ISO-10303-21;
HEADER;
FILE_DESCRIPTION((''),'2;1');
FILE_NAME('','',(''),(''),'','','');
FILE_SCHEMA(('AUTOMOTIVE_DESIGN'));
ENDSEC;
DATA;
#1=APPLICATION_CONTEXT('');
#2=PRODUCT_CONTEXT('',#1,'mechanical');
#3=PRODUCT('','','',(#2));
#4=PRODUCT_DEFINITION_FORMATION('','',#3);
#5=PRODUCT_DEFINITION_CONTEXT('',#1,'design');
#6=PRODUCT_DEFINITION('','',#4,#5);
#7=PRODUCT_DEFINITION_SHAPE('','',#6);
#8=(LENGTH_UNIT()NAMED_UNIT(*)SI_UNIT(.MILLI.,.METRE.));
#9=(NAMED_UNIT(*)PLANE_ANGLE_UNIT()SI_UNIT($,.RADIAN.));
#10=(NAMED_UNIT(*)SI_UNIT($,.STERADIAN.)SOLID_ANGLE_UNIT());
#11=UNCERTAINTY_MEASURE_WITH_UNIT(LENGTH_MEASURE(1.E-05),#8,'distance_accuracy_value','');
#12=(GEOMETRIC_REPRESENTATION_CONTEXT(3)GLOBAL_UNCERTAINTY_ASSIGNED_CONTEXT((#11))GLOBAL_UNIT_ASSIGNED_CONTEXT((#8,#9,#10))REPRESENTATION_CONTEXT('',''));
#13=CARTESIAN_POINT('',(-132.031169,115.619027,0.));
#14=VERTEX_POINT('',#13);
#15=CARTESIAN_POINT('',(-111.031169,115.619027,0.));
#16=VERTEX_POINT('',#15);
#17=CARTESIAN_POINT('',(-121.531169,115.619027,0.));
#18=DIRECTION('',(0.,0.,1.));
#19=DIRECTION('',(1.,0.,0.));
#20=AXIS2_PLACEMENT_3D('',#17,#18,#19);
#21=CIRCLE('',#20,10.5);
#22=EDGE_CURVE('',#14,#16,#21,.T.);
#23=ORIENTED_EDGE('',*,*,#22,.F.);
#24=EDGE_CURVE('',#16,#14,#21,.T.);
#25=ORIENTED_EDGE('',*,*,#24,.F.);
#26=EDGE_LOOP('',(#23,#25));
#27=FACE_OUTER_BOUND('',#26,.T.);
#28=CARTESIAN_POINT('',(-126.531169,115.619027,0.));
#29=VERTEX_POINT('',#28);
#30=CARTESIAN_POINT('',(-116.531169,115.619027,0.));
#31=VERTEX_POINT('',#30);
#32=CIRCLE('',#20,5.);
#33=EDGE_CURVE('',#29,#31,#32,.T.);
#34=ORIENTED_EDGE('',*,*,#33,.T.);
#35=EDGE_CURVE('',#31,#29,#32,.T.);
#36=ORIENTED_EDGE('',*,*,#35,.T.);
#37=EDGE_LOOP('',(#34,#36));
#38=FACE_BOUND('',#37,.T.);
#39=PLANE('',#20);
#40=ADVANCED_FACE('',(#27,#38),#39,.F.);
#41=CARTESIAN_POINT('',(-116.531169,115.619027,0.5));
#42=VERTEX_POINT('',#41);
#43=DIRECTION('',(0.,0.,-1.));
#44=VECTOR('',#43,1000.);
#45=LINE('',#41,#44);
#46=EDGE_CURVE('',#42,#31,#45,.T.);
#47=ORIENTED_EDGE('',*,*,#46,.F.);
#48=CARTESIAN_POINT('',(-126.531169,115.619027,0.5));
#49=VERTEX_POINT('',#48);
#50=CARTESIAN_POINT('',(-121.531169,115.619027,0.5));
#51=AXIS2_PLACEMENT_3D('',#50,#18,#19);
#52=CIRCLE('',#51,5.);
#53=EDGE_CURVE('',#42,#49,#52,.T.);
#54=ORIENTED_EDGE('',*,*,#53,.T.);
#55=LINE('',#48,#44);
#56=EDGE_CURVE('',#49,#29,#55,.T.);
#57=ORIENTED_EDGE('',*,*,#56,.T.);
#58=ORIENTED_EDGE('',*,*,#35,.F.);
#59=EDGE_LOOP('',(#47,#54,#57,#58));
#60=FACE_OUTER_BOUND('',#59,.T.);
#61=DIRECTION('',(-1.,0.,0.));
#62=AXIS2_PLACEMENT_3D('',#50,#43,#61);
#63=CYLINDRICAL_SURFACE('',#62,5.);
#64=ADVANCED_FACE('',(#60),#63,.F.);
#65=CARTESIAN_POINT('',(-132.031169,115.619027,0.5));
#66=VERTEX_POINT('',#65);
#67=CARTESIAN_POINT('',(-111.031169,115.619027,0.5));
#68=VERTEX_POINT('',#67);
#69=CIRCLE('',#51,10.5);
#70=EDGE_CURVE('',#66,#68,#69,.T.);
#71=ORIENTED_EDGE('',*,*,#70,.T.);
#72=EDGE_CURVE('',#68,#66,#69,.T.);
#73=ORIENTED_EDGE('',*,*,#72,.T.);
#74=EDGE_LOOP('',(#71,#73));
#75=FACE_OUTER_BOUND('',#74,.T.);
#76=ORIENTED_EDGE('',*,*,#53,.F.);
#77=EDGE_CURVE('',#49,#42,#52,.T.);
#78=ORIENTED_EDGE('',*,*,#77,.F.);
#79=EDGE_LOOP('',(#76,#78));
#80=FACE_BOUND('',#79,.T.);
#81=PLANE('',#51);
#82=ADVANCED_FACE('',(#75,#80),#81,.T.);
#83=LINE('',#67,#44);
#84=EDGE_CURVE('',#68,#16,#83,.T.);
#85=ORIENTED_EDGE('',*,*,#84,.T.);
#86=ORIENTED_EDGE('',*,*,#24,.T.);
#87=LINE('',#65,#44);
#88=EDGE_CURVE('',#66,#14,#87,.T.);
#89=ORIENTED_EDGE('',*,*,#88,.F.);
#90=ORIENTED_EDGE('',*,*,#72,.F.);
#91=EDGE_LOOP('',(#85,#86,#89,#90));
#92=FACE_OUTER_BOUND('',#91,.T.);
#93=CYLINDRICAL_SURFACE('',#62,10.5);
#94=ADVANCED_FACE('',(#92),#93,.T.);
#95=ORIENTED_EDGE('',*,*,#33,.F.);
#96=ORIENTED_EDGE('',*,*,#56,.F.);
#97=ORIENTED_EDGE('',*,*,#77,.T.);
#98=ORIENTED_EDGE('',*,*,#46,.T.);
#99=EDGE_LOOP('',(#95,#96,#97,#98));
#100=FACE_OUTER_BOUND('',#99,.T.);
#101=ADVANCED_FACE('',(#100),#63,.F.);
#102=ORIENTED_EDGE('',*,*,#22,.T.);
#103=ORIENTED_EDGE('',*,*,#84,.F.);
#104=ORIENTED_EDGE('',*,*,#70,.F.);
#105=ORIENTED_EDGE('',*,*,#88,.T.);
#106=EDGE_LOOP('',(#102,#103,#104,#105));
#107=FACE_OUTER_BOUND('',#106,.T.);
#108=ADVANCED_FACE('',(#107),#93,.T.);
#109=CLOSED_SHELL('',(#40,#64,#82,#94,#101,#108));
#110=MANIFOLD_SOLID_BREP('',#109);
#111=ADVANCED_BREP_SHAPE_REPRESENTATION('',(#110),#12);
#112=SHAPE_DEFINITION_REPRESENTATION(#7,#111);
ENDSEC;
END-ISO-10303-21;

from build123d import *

# Parameters (mm, degrees)
SKETCH1_R           = 10.5
SKETCH1_R_2         = 5
BOSS_EXTRUDE1_DEPTH = 0.5


with BuildPart() as part:
    # Sketch1 → Boss-Extrude1 (new body)
    with BuildSketch(Plane.XY):
        with Locations((-121.531169153, 115.619026916)):
            Circle(SKETCH1_R)
        with Locations((-121.531169153, 115.619026916)):
            Circle(SKETCH1_R_2, mode=Mode.SUBTRACT)
    extrude(amount=BOSS_EXTRUDE1_DEPTH)


solid = part.part
